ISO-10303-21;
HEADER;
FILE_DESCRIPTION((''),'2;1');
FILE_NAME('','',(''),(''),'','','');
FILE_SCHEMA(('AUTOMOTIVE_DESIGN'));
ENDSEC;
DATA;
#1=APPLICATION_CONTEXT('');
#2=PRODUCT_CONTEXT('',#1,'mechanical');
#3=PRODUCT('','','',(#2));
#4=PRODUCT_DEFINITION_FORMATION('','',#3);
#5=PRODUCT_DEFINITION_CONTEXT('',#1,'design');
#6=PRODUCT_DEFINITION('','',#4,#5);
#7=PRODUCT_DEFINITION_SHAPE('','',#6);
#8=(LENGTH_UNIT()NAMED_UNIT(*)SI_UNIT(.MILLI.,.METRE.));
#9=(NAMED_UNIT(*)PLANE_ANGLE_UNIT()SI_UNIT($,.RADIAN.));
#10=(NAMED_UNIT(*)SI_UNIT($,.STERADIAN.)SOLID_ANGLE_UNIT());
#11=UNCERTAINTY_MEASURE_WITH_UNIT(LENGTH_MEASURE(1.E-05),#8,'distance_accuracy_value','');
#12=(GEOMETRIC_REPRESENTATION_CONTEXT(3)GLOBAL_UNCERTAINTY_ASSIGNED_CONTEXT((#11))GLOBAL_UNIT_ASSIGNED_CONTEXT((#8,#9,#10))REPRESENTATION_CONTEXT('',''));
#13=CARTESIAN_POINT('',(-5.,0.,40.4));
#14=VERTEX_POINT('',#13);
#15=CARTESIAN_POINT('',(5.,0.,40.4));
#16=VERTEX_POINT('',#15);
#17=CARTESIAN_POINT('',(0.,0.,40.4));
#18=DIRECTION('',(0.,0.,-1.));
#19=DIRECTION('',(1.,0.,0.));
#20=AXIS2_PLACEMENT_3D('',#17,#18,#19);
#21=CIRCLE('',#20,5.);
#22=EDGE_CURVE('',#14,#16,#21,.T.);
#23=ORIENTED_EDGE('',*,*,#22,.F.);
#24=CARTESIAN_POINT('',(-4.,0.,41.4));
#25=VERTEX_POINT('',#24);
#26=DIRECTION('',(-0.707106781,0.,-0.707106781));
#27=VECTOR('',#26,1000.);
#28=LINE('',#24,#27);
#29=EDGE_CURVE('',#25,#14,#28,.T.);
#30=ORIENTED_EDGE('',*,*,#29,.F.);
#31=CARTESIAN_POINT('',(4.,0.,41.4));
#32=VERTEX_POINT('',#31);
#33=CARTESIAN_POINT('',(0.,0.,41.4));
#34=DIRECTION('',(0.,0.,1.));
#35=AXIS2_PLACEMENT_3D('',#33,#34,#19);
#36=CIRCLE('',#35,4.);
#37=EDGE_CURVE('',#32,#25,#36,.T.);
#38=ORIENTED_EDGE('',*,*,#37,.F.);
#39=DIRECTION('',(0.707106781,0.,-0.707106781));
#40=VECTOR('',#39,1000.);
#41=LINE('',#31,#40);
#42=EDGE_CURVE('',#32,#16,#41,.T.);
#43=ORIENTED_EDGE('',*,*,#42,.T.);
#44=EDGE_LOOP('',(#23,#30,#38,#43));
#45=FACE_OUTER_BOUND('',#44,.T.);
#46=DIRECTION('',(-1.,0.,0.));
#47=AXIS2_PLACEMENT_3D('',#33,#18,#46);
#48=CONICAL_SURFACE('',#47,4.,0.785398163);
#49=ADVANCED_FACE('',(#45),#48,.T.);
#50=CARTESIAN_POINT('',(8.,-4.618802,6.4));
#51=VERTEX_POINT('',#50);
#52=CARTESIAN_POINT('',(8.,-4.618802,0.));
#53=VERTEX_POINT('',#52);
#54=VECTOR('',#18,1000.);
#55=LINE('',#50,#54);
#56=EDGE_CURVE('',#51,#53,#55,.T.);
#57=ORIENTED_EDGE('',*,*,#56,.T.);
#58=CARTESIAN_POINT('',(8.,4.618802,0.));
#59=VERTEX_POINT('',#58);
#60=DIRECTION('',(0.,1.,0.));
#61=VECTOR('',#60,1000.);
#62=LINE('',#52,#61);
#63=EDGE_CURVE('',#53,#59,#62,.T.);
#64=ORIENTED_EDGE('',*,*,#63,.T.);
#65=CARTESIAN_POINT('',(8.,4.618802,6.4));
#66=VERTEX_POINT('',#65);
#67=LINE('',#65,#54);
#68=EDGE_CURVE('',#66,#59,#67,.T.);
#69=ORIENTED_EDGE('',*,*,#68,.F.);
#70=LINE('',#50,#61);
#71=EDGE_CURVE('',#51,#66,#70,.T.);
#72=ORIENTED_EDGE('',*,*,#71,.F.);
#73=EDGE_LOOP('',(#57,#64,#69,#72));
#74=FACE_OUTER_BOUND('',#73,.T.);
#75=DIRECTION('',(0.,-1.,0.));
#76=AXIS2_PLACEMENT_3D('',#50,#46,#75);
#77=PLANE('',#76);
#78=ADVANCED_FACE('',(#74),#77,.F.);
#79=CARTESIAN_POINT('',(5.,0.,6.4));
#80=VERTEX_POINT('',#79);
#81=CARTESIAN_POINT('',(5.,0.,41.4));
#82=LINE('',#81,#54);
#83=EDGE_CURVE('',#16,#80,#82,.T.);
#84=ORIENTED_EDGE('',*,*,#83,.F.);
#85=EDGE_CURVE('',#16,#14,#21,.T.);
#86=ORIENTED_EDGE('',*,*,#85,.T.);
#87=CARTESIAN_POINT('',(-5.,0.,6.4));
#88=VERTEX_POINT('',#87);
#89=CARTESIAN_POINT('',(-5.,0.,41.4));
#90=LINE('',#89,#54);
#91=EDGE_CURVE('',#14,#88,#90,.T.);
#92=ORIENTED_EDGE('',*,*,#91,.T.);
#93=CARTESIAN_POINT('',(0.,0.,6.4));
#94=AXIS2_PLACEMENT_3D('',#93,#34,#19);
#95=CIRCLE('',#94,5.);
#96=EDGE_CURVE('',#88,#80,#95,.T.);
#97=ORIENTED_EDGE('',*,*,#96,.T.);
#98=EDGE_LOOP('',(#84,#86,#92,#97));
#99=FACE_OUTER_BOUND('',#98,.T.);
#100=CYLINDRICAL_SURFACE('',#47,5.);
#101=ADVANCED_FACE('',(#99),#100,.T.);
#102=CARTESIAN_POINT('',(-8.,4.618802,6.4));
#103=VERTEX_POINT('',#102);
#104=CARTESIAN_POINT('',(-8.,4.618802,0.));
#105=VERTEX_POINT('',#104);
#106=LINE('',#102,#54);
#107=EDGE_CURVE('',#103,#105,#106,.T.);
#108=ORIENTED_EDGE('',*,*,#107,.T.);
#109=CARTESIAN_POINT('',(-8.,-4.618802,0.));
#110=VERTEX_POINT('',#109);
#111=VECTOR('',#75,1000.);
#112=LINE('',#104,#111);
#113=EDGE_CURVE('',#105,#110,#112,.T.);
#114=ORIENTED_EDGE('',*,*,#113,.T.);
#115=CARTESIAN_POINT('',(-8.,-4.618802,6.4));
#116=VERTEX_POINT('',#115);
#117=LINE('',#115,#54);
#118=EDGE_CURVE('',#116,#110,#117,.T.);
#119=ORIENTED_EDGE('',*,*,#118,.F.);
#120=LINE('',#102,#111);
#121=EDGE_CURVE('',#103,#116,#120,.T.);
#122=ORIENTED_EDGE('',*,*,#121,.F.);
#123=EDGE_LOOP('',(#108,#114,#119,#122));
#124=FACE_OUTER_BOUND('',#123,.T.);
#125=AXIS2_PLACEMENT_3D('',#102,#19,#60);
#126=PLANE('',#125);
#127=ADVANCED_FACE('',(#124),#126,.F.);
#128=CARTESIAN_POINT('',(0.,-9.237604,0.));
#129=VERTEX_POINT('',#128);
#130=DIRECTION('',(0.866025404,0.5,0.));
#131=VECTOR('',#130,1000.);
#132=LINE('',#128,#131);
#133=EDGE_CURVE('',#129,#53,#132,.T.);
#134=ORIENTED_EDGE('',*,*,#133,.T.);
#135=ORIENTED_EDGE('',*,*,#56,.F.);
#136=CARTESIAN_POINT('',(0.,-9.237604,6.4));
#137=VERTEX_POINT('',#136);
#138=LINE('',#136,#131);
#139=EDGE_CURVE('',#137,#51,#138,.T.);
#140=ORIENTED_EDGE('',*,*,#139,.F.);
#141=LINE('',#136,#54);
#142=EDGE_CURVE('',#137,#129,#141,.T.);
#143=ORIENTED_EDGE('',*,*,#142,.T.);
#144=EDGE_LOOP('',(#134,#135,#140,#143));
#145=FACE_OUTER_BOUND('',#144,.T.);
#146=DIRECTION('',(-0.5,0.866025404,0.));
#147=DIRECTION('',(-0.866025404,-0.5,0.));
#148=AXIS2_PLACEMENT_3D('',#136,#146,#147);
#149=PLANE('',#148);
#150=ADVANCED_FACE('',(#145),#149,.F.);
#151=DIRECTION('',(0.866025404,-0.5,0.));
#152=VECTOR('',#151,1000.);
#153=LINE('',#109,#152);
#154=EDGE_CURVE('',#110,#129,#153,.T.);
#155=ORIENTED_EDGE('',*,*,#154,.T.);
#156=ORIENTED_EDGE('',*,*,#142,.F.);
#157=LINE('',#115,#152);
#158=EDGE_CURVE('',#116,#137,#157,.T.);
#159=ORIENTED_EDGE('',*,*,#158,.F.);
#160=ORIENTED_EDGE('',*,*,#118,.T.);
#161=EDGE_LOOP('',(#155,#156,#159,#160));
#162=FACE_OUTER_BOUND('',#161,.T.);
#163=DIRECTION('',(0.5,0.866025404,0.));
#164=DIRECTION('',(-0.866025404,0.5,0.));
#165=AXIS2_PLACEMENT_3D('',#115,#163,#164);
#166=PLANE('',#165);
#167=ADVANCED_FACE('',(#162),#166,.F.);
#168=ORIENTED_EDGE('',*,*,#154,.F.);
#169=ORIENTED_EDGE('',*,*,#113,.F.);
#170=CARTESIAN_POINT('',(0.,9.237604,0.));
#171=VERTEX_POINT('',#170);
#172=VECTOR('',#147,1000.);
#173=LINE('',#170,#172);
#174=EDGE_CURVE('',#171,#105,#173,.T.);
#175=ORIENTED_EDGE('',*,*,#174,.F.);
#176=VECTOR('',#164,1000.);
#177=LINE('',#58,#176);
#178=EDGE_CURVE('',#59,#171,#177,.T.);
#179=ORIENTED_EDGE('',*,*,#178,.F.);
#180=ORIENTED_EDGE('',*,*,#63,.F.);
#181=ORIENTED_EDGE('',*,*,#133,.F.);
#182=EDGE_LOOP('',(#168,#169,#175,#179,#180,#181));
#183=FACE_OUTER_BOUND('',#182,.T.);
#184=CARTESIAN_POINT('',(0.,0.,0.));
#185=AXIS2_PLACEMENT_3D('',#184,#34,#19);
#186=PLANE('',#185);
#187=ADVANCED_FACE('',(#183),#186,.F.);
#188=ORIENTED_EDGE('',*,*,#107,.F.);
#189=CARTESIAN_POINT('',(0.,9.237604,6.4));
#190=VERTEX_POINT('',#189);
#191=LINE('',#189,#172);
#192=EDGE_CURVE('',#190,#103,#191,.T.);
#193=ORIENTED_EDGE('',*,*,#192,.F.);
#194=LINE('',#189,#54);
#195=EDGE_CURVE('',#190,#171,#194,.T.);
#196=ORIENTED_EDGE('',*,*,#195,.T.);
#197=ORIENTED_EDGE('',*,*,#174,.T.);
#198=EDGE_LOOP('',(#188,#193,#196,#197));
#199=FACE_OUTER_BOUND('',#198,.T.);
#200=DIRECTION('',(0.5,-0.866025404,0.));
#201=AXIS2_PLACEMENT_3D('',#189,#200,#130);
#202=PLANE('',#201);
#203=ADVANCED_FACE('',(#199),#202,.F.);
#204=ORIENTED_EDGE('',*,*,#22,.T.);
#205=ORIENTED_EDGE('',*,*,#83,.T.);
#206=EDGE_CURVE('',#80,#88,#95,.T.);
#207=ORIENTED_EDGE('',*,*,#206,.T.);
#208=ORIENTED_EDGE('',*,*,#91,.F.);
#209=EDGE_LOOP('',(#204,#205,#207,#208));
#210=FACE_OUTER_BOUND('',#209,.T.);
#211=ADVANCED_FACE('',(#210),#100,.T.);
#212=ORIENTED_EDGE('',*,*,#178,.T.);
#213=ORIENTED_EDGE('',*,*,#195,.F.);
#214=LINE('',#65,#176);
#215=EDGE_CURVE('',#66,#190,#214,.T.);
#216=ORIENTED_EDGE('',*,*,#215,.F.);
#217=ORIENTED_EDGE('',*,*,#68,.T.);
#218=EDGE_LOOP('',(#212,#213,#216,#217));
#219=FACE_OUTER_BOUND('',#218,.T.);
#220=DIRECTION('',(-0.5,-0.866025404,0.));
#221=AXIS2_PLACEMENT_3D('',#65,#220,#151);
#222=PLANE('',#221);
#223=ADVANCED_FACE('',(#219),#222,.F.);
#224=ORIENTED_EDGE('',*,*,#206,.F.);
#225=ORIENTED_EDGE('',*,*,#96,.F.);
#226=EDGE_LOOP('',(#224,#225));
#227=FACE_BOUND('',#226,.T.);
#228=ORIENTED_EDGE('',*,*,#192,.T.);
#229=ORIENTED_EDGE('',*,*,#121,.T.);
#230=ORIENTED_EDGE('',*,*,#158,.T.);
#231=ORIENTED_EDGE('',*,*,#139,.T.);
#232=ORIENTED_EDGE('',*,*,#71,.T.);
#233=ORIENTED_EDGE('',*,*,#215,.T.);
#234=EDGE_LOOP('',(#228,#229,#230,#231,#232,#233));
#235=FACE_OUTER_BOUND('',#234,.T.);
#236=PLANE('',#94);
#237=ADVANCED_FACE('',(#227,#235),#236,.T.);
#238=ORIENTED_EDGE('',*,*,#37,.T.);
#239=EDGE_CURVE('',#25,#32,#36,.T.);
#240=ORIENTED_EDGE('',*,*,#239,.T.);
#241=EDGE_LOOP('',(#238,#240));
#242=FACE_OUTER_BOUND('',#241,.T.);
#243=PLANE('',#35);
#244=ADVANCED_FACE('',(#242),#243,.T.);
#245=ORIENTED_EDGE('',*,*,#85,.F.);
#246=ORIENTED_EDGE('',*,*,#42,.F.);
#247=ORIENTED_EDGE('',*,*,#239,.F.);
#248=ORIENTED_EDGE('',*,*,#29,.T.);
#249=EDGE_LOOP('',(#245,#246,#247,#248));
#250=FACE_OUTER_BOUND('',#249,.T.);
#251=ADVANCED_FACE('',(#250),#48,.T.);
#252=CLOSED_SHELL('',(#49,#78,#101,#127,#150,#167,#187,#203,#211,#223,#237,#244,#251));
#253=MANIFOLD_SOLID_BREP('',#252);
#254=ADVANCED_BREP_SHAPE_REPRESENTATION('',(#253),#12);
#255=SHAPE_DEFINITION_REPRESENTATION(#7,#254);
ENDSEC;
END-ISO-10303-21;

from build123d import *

# Parameters (mm, degrees)
BOSS_EXTRUDE1_DEPTH = 6.4
SKETCH3_R           = 5
BOSS_EXTRUDE2_DEPTH = 35
CHAMFER1_SIZE       = 1


with BuildPart() as part:
    # Sketch1 → Boss-Extrude1 (new body)
    with BuildSketch(Plane.XY):
        Polygon((8, 4.618802154), (0, 9.237604307), (-8, 4.618802154), (-8, -4.618802154), (0, -9.237604307), (8, -4.618802154), align=None)
    extrude(amount=BOSS_EXTRUDE1_DEPTH)

    # Sketch3 → Boss-Extrude2 (add)
    with BuildSketch(Plane.XY.offset(6.4)):
        Circle(SKETCH3_R)
    extrude(amount=BOSS_EXTRUDE2_DEPTH)

    # Chamfer1
    chamfer1_edges = [part.edges().sort_by_distance(p)[0] for p in [
        (-5, 0, 41.4),
    ]]
    chamfer(chamfer1_edges, length=CHAMFER1_SIZE)


solid = part.part
